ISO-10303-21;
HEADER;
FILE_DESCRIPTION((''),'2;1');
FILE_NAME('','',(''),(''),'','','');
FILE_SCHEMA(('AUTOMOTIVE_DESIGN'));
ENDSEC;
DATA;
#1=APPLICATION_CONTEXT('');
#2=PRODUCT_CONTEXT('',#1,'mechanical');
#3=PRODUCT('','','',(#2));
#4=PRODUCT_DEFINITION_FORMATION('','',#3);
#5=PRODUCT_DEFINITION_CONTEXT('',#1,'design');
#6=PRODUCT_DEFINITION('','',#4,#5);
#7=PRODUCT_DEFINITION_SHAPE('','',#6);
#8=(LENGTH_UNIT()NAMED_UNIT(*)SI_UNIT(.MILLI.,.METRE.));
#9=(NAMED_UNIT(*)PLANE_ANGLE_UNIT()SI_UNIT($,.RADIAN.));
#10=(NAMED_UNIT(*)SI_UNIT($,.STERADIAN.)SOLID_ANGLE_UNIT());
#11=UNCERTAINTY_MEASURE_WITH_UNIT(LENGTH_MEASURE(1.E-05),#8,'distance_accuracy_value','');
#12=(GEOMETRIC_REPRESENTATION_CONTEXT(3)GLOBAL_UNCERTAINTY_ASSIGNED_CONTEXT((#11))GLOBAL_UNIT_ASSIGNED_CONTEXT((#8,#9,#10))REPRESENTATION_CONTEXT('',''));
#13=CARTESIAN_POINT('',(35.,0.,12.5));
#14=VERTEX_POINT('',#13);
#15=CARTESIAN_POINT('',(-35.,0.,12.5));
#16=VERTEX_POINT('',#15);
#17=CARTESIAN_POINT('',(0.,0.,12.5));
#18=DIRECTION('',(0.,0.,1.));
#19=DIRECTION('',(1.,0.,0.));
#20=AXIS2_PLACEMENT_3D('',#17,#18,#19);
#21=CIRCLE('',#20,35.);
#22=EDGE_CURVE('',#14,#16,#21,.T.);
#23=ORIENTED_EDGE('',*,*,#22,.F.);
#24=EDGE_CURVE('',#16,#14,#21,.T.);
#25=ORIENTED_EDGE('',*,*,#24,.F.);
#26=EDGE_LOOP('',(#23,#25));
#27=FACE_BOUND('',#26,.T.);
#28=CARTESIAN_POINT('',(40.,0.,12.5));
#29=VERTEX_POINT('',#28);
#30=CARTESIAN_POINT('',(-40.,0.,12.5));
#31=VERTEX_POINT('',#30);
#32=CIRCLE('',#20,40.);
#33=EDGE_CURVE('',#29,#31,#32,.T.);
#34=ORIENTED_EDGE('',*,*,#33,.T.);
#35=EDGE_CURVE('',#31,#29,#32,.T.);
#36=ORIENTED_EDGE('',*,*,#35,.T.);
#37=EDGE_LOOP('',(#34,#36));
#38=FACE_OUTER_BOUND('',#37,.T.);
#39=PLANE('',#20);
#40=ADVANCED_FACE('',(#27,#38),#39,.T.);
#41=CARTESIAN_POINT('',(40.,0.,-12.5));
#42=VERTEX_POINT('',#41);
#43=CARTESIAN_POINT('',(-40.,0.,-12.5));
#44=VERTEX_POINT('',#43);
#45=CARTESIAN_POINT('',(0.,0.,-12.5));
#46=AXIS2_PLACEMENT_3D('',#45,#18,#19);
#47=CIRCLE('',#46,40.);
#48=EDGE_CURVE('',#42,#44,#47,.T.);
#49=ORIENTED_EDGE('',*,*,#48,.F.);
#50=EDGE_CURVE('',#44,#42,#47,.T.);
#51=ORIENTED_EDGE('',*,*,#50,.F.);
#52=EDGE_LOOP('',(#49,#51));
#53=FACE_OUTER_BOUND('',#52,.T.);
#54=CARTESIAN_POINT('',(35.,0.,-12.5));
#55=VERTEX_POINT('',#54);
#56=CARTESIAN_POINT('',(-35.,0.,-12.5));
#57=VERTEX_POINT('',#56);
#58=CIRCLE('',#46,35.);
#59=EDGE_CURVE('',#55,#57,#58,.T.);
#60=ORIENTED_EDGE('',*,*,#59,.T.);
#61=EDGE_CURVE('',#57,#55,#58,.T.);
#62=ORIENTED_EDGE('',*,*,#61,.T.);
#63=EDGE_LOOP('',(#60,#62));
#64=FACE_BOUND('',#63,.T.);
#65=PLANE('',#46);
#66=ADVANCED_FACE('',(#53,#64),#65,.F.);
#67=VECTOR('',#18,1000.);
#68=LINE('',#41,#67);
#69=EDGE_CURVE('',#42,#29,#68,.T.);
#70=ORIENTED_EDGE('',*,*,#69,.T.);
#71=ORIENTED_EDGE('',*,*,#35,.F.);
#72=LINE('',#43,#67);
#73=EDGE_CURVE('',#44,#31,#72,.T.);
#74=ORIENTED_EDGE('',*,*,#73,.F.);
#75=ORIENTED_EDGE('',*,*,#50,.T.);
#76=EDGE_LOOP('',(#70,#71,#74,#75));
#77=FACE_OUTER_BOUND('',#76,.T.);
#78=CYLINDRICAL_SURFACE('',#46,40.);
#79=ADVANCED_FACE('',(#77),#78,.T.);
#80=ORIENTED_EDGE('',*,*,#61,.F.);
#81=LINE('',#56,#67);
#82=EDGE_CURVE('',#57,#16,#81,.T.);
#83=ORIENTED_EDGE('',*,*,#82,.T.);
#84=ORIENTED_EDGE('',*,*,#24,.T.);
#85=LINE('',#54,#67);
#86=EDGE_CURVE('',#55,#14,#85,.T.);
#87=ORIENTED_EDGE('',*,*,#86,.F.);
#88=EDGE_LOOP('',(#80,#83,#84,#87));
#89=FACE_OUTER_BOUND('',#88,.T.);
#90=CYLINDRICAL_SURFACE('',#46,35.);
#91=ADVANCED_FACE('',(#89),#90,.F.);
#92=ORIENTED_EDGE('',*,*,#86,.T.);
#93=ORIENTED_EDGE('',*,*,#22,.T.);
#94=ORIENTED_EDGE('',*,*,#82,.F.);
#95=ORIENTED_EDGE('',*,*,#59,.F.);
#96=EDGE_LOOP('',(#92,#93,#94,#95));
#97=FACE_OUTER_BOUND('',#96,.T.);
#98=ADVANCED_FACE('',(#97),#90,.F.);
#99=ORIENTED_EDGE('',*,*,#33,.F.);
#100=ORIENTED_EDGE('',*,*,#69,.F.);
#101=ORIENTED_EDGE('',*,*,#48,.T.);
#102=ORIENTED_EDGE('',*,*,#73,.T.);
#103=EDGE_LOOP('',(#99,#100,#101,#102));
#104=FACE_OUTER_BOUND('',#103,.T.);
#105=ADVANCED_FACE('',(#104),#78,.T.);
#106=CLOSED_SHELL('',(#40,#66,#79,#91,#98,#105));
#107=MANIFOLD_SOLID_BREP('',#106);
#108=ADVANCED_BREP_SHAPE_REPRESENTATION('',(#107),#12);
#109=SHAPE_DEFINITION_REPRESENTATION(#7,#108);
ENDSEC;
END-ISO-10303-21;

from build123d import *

# Parameters (mm, degrees)
SKETCH_1_R      = 40
SKETCH_1_R_2    = 35
EXTRUDE_1_DEPTH = 12.5


with BuildPart() as part:
    # 草图1 → 凸台-拉伸1 (new, symmetric)
    with BuildSketch(Plane.XY):
        Circle(SKETCH_1_R)
        Circle(SKETCH_1_R_2, mode=Mode.SUBTRACT)
    extrude(amount=EXTRUDE_1_DEPTH, both=True)


solid = part.part
